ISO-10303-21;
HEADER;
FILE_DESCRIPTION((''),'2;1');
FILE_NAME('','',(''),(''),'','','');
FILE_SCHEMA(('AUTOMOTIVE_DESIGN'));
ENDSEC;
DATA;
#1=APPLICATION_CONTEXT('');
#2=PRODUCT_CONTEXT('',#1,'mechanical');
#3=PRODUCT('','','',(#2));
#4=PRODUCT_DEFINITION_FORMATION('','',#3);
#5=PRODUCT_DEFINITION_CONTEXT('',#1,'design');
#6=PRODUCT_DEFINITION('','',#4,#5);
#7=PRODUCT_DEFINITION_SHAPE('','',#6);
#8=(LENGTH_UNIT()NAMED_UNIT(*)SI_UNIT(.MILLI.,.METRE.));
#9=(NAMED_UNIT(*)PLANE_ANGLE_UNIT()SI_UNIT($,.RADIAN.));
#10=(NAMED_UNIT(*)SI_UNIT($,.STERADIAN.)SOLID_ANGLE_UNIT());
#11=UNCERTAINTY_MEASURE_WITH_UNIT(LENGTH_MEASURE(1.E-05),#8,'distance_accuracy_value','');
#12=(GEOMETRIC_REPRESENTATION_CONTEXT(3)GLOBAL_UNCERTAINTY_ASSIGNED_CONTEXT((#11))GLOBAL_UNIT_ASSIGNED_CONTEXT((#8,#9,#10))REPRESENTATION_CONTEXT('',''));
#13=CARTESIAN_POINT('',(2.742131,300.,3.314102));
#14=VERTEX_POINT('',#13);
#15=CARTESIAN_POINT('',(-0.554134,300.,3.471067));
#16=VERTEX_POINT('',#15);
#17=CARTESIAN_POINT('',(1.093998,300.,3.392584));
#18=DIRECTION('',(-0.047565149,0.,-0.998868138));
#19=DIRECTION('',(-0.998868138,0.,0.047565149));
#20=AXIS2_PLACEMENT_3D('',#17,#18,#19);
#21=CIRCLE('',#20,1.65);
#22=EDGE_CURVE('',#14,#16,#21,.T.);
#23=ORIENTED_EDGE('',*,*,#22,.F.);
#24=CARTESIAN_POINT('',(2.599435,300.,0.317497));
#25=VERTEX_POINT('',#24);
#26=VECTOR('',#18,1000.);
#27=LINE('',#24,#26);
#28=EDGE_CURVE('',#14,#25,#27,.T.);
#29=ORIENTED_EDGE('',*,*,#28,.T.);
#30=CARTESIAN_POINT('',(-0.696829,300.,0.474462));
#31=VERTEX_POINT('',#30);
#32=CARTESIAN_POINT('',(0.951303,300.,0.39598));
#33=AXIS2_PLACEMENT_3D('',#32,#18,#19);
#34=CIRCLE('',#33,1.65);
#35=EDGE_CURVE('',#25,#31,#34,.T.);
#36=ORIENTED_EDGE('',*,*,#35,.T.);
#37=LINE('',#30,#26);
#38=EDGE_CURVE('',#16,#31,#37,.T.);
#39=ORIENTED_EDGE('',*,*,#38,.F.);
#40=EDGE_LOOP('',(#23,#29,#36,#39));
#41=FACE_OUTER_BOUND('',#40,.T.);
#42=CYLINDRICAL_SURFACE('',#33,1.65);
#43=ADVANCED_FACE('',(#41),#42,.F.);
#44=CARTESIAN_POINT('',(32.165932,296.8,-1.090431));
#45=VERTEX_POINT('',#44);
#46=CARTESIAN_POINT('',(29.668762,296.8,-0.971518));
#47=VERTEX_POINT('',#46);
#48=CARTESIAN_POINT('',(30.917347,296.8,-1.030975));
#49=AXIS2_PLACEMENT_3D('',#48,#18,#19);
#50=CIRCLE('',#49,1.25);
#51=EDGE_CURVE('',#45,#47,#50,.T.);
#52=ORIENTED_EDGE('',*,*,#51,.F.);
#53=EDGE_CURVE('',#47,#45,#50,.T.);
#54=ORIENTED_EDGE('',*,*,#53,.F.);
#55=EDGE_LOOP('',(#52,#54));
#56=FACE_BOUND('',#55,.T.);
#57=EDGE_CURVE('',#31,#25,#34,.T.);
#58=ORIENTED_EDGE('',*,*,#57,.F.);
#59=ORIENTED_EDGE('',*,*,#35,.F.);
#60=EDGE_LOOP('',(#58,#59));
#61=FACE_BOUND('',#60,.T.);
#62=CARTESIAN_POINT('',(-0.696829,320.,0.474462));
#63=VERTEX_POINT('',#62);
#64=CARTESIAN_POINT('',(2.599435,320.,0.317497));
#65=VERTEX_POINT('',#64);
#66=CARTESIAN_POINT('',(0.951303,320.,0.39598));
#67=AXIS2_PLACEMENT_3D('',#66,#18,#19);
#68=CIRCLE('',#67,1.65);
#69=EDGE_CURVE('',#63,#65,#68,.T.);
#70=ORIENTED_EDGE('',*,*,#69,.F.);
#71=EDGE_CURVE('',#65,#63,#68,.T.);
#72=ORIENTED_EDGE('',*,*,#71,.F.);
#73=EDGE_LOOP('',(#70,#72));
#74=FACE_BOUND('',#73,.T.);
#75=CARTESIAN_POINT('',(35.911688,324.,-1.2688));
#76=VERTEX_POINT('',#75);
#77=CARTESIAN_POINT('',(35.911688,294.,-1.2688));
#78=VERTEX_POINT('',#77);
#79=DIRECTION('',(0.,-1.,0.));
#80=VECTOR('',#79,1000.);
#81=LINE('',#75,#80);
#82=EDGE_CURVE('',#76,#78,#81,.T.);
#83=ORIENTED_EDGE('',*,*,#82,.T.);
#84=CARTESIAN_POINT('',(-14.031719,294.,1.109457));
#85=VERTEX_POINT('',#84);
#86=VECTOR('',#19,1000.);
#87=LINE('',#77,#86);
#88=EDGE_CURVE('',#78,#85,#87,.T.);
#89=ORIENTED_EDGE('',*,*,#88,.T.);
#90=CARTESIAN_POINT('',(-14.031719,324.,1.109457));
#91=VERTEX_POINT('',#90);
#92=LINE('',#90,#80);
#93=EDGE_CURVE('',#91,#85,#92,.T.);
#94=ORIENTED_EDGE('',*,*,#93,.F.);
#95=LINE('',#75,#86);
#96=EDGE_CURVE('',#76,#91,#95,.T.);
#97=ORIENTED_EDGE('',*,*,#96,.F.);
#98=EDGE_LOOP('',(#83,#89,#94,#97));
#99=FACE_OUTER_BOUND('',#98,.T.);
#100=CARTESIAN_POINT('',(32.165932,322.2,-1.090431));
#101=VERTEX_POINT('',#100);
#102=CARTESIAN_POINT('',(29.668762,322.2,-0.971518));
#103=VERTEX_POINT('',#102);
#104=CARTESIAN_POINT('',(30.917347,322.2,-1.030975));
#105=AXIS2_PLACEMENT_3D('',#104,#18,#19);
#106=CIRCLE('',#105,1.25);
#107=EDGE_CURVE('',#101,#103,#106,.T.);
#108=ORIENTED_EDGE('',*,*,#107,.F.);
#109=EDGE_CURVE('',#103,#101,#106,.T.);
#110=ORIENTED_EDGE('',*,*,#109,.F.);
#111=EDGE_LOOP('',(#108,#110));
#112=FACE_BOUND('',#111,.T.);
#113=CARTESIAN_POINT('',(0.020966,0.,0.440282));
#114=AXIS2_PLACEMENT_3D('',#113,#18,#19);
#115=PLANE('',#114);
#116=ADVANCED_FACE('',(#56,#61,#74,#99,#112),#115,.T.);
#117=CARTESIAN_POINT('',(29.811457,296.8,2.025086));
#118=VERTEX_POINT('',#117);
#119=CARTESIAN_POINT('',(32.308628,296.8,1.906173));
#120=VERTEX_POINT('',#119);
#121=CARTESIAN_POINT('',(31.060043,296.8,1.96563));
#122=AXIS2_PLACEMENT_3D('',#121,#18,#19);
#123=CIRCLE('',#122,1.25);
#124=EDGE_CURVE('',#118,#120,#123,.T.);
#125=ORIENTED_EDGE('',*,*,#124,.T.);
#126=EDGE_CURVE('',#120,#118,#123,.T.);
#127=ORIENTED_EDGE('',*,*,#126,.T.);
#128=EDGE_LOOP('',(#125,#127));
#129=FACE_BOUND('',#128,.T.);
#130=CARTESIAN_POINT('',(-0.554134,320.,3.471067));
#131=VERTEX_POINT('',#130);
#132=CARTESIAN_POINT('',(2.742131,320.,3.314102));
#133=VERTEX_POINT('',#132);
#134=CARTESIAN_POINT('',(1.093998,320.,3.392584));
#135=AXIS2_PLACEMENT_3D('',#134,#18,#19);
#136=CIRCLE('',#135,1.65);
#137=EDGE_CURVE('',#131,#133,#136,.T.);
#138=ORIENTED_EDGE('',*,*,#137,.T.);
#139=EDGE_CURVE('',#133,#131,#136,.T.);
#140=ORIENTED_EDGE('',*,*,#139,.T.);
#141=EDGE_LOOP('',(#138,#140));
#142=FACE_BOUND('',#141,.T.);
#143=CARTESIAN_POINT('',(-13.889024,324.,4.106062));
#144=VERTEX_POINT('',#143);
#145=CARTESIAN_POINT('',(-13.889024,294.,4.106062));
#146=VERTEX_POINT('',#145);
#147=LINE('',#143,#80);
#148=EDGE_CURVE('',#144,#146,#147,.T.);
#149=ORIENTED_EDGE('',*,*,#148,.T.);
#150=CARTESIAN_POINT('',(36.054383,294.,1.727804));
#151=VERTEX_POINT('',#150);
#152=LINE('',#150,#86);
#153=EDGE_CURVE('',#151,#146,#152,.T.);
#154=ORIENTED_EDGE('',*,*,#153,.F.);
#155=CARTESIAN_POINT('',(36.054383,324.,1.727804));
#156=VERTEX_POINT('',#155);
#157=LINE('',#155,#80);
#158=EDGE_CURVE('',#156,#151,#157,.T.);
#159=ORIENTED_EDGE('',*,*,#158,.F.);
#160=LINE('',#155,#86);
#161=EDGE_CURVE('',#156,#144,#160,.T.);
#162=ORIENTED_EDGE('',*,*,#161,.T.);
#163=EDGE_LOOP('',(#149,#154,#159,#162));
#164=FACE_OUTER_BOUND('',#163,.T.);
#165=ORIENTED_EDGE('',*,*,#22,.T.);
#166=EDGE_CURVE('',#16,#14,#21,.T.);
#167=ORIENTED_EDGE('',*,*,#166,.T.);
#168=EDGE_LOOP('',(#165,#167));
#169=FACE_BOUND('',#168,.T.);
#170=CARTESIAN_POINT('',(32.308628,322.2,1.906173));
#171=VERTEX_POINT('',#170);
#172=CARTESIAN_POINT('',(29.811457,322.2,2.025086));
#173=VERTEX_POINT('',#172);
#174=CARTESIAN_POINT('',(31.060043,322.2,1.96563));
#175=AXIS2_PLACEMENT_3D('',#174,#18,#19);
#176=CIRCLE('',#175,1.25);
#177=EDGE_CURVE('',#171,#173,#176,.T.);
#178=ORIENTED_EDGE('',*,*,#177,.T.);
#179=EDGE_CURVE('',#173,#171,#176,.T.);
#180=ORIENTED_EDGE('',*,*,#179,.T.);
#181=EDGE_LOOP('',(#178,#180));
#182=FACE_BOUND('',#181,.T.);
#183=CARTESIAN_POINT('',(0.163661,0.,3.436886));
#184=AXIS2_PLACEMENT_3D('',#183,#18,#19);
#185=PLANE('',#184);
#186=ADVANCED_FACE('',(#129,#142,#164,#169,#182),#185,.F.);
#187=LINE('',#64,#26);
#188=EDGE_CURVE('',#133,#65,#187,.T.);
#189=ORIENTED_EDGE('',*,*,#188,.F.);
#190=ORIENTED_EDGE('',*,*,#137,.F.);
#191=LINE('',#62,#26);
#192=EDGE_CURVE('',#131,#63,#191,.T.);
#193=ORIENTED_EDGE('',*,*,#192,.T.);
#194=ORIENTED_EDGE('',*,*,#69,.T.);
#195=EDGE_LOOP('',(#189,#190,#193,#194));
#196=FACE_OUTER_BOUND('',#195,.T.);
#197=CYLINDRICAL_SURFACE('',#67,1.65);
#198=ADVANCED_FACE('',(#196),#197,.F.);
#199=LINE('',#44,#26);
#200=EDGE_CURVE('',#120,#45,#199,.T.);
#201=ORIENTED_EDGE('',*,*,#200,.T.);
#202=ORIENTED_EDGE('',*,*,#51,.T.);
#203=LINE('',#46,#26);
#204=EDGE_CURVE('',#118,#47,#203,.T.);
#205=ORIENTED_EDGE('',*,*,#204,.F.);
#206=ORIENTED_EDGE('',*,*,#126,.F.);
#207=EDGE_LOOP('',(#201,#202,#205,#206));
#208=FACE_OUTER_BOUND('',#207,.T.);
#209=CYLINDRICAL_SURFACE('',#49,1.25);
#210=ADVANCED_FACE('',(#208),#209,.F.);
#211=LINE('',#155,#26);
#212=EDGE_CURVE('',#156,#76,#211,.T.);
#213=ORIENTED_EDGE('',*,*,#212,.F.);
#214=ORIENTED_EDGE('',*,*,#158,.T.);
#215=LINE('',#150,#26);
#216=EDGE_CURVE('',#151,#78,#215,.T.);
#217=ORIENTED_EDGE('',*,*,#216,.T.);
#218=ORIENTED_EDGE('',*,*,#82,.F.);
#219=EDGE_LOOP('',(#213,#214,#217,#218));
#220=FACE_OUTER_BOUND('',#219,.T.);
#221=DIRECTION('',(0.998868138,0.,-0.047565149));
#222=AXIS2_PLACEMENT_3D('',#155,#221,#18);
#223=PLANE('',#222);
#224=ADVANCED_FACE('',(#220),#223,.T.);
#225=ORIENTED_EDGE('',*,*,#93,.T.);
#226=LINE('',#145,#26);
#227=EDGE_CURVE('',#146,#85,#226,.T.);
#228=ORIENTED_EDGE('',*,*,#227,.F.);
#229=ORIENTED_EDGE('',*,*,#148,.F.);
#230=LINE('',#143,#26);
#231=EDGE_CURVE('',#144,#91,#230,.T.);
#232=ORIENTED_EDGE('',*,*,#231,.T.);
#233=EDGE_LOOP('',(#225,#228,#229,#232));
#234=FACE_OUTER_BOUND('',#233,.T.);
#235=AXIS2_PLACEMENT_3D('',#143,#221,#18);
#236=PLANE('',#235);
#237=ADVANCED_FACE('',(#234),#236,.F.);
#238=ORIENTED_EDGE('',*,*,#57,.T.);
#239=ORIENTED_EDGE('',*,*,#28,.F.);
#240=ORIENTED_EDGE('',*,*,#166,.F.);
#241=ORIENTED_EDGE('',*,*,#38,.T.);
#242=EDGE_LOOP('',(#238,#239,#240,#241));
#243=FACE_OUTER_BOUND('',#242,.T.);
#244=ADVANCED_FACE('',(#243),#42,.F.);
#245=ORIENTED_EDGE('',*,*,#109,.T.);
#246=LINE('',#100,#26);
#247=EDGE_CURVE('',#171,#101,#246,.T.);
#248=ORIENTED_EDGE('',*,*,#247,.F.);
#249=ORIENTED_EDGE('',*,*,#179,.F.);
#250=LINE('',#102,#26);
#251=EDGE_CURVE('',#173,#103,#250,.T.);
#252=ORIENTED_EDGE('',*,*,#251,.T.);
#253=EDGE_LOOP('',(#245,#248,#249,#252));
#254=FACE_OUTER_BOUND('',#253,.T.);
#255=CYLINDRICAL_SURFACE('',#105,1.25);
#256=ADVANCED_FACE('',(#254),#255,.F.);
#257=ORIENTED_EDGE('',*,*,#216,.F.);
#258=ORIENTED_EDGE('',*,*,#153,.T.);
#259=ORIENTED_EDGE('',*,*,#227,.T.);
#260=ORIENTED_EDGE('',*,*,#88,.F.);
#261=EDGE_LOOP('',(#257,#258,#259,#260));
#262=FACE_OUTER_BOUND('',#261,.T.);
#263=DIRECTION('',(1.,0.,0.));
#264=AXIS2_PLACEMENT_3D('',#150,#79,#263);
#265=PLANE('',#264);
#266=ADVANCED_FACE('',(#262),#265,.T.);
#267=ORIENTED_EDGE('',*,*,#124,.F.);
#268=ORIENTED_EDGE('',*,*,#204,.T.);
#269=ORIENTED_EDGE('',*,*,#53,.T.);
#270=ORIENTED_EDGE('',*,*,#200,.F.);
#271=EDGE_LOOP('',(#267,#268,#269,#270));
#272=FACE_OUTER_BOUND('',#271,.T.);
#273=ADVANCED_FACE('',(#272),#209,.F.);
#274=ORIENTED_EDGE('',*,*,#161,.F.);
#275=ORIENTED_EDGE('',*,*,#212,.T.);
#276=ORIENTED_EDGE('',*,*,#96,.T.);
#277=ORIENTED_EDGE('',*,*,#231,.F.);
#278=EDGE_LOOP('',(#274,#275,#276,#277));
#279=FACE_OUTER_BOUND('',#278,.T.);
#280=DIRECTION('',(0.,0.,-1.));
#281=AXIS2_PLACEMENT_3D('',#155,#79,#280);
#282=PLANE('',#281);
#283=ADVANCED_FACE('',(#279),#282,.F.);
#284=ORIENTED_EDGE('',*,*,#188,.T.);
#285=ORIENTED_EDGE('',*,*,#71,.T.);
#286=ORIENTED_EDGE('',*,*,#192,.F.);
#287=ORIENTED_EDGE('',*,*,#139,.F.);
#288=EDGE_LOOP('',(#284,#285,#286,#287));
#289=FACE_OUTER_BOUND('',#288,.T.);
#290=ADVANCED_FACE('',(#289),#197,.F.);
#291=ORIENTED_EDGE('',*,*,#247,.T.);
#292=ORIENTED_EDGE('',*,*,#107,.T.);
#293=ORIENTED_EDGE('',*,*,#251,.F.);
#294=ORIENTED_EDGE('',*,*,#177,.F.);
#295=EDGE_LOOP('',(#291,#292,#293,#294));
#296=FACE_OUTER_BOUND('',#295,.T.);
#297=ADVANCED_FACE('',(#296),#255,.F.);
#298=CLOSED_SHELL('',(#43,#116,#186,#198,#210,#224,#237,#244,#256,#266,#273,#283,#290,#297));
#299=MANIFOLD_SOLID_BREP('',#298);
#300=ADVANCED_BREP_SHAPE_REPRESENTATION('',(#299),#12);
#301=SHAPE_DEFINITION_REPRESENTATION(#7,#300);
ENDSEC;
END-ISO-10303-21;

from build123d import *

# Parameters (mm, degrees)
SKETCH1_W           = 50
SKETCH1_H           = 30
BOSS_EXTRUDE1_DEPTH = 3
M4_TAPPED_HOLE1_D   = 3.3
M3_TAPPED_HOLE1_D   = 2.5


with BuildPart() as part:
    # Sketch1 → Boss-Extrude1 (new body)
    with BuildSketch(Plane(origin=(18.523271638, 0, -0.440780543), x_dir=(-0.9988681377244376, 0, 0.04756514941544916), z_dir=(-0.04756514941544916, 0, -0.9988681377244377))):
        with Locations((7.591880235, 309)):
            Rectangle(SKETCH1_W, SKETCH1_H)
    extrude(amount=-BOSS_EXTRUDE1_DEPTH)

    # M4 Tapped Hole1 (through all)
    with Locations(Plane(origin=(0.020965792, 0, 0.44028164), x_dir=(-0.9988681377244376, 0, 0.04756514941544917), z_dir=(-0.047565149415449176, 0, -0.9988681377244377))):
        with Locations((-0.931391403, 320), (-0.931391403, 300)):
            Hole(M4_TAPPED_HOLE1_D / 2)

    # M3 Tapped Hole1 (through all)
    with Locations(Plane(origin=(0.020965792, 0, 0.44028164), x_dir=(-0.9988681377244376, 0, 0.04756514941544917), z_dir=(-0.047565149415449176, 0, -0.9988681377244377))):
        with Locations((-30.931391403, 322.2), (-30.931391403, 296.8)):
            Hole(M3_TAPPED_HOLE1_D / 2)


solid = part.part
